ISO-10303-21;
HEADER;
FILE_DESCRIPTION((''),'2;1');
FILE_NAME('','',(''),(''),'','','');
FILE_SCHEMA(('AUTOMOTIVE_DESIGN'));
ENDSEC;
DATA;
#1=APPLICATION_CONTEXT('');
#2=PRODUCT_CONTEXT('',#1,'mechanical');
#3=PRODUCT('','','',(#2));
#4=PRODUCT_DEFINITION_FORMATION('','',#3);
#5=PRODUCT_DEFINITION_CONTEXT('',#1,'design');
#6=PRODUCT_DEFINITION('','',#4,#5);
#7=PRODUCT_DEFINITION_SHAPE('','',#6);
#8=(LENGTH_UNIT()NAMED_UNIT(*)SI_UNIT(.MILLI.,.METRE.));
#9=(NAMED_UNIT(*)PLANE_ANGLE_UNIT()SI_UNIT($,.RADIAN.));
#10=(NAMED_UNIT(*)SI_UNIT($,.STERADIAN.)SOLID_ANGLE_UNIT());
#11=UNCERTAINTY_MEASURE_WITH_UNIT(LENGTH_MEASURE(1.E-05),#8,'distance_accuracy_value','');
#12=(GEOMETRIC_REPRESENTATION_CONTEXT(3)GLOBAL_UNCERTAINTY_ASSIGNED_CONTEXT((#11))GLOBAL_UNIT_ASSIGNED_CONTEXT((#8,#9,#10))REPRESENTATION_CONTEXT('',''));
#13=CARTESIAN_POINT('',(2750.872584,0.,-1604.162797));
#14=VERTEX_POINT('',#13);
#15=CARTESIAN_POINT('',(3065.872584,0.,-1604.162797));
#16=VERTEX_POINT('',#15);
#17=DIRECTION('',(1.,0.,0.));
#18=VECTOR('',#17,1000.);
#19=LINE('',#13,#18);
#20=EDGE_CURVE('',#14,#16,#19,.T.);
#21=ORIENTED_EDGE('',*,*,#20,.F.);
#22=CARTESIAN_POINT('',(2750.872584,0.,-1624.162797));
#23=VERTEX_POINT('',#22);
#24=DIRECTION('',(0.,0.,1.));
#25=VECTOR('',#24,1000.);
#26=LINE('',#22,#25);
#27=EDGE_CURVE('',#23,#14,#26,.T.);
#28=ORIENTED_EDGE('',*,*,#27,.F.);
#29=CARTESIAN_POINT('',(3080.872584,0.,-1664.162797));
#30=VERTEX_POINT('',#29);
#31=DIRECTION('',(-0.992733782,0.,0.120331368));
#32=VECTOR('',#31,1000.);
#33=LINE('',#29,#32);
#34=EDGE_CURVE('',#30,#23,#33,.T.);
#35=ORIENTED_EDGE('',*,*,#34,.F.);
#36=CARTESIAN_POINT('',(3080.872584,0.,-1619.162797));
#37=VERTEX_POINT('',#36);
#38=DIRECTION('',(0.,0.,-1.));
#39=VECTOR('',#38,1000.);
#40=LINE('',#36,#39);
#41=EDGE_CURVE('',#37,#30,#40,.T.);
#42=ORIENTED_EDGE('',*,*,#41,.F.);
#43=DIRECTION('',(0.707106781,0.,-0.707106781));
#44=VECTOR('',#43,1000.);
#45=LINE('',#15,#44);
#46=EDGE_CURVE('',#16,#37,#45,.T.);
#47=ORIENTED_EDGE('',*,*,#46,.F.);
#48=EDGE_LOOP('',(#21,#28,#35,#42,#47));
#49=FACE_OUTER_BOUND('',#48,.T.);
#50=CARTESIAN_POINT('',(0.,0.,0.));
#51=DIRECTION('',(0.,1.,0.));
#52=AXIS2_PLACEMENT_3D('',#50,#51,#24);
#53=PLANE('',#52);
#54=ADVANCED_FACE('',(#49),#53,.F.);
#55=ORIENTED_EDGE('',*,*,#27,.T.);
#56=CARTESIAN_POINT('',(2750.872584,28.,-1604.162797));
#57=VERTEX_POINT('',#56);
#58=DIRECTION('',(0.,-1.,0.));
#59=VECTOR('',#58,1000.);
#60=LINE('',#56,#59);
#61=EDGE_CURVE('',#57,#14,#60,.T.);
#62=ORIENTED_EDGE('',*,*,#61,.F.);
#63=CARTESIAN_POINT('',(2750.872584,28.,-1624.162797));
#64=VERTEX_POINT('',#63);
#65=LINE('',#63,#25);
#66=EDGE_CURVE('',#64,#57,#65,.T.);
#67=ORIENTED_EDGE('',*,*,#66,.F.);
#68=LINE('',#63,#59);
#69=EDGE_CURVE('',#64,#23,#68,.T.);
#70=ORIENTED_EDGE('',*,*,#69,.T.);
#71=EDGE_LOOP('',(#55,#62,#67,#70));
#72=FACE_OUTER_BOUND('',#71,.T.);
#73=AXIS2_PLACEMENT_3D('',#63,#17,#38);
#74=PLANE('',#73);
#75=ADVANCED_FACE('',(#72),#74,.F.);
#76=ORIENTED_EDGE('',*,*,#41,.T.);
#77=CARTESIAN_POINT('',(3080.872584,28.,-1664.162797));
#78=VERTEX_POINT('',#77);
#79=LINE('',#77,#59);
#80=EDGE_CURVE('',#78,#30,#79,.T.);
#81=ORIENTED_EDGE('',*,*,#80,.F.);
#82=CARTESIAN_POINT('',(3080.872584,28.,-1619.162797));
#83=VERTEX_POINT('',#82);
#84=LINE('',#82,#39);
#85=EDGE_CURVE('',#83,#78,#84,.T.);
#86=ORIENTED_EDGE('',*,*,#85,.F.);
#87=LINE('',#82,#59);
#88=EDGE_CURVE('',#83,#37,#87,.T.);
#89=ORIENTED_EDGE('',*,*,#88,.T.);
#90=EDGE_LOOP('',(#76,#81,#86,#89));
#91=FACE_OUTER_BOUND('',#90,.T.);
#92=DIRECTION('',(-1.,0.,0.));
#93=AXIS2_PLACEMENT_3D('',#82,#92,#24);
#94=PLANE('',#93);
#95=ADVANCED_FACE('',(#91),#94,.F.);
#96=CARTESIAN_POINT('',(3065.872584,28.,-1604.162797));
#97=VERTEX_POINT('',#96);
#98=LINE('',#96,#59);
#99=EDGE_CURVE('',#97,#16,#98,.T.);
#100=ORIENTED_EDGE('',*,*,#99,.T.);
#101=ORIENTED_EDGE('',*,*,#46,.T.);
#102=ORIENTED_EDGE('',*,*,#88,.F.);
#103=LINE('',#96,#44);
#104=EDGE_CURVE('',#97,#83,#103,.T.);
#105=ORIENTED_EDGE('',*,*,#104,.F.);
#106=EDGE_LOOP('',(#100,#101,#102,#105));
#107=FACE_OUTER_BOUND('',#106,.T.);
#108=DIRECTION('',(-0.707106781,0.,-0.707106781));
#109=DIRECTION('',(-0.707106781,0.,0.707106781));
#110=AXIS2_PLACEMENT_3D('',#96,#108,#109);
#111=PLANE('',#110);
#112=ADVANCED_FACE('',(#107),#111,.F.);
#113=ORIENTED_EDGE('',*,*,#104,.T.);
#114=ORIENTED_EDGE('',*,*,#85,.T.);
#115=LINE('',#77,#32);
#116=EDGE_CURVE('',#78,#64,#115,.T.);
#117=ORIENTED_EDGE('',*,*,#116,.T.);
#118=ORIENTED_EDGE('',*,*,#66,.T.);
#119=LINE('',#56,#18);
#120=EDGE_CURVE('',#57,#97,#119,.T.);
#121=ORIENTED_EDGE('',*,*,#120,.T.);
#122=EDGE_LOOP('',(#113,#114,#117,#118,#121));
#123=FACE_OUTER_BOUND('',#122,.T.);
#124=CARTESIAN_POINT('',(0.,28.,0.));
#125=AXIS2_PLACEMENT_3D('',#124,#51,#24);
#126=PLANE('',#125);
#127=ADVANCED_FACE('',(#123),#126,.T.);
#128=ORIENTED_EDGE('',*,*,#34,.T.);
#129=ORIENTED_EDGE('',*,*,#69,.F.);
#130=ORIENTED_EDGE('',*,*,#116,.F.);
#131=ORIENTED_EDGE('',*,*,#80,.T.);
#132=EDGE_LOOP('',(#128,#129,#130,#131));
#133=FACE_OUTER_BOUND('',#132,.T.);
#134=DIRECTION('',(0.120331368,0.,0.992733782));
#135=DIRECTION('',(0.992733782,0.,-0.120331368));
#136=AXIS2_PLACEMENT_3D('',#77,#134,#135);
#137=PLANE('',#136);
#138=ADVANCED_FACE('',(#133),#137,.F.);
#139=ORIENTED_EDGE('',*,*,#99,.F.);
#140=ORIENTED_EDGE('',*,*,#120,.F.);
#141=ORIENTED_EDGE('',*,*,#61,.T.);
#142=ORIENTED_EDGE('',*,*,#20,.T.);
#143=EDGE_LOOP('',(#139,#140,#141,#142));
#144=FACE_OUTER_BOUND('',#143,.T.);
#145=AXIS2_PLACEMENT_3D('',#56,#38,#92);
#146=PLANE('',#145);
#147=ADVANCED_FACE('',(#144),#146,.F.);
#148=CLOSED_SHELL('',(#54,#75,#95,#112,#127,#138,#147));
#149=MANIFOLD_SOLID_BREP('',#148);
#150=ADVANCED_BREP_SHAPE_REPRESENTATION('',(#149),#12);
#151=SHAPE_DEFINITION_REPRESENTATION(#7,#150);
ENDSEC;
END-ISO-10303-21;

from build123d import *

# Parameters (mm, degrees)
BOSS_EXTRUDE1_DEPTH = 28


with BuildPart() as part:
    # Sketch1 → Boss-Extrude1 (new body)
    with BuildSketch(Plane(origin=(0, 0, 0), x_dir=(1, 0, 0), z_dir=(0, 1, 0))):
        Polygon((2750.872583656, 1604.162796977), (3065.872583656, 1604.162796977), (3080.872583656, 1619.162796977), (3080.872583656, 1664.162796977), (2750.872583656, 1624.162796977), align=None)
    extrude(amount=BOSS_EXTRUDE1_DEPTH)


solid = part.part
